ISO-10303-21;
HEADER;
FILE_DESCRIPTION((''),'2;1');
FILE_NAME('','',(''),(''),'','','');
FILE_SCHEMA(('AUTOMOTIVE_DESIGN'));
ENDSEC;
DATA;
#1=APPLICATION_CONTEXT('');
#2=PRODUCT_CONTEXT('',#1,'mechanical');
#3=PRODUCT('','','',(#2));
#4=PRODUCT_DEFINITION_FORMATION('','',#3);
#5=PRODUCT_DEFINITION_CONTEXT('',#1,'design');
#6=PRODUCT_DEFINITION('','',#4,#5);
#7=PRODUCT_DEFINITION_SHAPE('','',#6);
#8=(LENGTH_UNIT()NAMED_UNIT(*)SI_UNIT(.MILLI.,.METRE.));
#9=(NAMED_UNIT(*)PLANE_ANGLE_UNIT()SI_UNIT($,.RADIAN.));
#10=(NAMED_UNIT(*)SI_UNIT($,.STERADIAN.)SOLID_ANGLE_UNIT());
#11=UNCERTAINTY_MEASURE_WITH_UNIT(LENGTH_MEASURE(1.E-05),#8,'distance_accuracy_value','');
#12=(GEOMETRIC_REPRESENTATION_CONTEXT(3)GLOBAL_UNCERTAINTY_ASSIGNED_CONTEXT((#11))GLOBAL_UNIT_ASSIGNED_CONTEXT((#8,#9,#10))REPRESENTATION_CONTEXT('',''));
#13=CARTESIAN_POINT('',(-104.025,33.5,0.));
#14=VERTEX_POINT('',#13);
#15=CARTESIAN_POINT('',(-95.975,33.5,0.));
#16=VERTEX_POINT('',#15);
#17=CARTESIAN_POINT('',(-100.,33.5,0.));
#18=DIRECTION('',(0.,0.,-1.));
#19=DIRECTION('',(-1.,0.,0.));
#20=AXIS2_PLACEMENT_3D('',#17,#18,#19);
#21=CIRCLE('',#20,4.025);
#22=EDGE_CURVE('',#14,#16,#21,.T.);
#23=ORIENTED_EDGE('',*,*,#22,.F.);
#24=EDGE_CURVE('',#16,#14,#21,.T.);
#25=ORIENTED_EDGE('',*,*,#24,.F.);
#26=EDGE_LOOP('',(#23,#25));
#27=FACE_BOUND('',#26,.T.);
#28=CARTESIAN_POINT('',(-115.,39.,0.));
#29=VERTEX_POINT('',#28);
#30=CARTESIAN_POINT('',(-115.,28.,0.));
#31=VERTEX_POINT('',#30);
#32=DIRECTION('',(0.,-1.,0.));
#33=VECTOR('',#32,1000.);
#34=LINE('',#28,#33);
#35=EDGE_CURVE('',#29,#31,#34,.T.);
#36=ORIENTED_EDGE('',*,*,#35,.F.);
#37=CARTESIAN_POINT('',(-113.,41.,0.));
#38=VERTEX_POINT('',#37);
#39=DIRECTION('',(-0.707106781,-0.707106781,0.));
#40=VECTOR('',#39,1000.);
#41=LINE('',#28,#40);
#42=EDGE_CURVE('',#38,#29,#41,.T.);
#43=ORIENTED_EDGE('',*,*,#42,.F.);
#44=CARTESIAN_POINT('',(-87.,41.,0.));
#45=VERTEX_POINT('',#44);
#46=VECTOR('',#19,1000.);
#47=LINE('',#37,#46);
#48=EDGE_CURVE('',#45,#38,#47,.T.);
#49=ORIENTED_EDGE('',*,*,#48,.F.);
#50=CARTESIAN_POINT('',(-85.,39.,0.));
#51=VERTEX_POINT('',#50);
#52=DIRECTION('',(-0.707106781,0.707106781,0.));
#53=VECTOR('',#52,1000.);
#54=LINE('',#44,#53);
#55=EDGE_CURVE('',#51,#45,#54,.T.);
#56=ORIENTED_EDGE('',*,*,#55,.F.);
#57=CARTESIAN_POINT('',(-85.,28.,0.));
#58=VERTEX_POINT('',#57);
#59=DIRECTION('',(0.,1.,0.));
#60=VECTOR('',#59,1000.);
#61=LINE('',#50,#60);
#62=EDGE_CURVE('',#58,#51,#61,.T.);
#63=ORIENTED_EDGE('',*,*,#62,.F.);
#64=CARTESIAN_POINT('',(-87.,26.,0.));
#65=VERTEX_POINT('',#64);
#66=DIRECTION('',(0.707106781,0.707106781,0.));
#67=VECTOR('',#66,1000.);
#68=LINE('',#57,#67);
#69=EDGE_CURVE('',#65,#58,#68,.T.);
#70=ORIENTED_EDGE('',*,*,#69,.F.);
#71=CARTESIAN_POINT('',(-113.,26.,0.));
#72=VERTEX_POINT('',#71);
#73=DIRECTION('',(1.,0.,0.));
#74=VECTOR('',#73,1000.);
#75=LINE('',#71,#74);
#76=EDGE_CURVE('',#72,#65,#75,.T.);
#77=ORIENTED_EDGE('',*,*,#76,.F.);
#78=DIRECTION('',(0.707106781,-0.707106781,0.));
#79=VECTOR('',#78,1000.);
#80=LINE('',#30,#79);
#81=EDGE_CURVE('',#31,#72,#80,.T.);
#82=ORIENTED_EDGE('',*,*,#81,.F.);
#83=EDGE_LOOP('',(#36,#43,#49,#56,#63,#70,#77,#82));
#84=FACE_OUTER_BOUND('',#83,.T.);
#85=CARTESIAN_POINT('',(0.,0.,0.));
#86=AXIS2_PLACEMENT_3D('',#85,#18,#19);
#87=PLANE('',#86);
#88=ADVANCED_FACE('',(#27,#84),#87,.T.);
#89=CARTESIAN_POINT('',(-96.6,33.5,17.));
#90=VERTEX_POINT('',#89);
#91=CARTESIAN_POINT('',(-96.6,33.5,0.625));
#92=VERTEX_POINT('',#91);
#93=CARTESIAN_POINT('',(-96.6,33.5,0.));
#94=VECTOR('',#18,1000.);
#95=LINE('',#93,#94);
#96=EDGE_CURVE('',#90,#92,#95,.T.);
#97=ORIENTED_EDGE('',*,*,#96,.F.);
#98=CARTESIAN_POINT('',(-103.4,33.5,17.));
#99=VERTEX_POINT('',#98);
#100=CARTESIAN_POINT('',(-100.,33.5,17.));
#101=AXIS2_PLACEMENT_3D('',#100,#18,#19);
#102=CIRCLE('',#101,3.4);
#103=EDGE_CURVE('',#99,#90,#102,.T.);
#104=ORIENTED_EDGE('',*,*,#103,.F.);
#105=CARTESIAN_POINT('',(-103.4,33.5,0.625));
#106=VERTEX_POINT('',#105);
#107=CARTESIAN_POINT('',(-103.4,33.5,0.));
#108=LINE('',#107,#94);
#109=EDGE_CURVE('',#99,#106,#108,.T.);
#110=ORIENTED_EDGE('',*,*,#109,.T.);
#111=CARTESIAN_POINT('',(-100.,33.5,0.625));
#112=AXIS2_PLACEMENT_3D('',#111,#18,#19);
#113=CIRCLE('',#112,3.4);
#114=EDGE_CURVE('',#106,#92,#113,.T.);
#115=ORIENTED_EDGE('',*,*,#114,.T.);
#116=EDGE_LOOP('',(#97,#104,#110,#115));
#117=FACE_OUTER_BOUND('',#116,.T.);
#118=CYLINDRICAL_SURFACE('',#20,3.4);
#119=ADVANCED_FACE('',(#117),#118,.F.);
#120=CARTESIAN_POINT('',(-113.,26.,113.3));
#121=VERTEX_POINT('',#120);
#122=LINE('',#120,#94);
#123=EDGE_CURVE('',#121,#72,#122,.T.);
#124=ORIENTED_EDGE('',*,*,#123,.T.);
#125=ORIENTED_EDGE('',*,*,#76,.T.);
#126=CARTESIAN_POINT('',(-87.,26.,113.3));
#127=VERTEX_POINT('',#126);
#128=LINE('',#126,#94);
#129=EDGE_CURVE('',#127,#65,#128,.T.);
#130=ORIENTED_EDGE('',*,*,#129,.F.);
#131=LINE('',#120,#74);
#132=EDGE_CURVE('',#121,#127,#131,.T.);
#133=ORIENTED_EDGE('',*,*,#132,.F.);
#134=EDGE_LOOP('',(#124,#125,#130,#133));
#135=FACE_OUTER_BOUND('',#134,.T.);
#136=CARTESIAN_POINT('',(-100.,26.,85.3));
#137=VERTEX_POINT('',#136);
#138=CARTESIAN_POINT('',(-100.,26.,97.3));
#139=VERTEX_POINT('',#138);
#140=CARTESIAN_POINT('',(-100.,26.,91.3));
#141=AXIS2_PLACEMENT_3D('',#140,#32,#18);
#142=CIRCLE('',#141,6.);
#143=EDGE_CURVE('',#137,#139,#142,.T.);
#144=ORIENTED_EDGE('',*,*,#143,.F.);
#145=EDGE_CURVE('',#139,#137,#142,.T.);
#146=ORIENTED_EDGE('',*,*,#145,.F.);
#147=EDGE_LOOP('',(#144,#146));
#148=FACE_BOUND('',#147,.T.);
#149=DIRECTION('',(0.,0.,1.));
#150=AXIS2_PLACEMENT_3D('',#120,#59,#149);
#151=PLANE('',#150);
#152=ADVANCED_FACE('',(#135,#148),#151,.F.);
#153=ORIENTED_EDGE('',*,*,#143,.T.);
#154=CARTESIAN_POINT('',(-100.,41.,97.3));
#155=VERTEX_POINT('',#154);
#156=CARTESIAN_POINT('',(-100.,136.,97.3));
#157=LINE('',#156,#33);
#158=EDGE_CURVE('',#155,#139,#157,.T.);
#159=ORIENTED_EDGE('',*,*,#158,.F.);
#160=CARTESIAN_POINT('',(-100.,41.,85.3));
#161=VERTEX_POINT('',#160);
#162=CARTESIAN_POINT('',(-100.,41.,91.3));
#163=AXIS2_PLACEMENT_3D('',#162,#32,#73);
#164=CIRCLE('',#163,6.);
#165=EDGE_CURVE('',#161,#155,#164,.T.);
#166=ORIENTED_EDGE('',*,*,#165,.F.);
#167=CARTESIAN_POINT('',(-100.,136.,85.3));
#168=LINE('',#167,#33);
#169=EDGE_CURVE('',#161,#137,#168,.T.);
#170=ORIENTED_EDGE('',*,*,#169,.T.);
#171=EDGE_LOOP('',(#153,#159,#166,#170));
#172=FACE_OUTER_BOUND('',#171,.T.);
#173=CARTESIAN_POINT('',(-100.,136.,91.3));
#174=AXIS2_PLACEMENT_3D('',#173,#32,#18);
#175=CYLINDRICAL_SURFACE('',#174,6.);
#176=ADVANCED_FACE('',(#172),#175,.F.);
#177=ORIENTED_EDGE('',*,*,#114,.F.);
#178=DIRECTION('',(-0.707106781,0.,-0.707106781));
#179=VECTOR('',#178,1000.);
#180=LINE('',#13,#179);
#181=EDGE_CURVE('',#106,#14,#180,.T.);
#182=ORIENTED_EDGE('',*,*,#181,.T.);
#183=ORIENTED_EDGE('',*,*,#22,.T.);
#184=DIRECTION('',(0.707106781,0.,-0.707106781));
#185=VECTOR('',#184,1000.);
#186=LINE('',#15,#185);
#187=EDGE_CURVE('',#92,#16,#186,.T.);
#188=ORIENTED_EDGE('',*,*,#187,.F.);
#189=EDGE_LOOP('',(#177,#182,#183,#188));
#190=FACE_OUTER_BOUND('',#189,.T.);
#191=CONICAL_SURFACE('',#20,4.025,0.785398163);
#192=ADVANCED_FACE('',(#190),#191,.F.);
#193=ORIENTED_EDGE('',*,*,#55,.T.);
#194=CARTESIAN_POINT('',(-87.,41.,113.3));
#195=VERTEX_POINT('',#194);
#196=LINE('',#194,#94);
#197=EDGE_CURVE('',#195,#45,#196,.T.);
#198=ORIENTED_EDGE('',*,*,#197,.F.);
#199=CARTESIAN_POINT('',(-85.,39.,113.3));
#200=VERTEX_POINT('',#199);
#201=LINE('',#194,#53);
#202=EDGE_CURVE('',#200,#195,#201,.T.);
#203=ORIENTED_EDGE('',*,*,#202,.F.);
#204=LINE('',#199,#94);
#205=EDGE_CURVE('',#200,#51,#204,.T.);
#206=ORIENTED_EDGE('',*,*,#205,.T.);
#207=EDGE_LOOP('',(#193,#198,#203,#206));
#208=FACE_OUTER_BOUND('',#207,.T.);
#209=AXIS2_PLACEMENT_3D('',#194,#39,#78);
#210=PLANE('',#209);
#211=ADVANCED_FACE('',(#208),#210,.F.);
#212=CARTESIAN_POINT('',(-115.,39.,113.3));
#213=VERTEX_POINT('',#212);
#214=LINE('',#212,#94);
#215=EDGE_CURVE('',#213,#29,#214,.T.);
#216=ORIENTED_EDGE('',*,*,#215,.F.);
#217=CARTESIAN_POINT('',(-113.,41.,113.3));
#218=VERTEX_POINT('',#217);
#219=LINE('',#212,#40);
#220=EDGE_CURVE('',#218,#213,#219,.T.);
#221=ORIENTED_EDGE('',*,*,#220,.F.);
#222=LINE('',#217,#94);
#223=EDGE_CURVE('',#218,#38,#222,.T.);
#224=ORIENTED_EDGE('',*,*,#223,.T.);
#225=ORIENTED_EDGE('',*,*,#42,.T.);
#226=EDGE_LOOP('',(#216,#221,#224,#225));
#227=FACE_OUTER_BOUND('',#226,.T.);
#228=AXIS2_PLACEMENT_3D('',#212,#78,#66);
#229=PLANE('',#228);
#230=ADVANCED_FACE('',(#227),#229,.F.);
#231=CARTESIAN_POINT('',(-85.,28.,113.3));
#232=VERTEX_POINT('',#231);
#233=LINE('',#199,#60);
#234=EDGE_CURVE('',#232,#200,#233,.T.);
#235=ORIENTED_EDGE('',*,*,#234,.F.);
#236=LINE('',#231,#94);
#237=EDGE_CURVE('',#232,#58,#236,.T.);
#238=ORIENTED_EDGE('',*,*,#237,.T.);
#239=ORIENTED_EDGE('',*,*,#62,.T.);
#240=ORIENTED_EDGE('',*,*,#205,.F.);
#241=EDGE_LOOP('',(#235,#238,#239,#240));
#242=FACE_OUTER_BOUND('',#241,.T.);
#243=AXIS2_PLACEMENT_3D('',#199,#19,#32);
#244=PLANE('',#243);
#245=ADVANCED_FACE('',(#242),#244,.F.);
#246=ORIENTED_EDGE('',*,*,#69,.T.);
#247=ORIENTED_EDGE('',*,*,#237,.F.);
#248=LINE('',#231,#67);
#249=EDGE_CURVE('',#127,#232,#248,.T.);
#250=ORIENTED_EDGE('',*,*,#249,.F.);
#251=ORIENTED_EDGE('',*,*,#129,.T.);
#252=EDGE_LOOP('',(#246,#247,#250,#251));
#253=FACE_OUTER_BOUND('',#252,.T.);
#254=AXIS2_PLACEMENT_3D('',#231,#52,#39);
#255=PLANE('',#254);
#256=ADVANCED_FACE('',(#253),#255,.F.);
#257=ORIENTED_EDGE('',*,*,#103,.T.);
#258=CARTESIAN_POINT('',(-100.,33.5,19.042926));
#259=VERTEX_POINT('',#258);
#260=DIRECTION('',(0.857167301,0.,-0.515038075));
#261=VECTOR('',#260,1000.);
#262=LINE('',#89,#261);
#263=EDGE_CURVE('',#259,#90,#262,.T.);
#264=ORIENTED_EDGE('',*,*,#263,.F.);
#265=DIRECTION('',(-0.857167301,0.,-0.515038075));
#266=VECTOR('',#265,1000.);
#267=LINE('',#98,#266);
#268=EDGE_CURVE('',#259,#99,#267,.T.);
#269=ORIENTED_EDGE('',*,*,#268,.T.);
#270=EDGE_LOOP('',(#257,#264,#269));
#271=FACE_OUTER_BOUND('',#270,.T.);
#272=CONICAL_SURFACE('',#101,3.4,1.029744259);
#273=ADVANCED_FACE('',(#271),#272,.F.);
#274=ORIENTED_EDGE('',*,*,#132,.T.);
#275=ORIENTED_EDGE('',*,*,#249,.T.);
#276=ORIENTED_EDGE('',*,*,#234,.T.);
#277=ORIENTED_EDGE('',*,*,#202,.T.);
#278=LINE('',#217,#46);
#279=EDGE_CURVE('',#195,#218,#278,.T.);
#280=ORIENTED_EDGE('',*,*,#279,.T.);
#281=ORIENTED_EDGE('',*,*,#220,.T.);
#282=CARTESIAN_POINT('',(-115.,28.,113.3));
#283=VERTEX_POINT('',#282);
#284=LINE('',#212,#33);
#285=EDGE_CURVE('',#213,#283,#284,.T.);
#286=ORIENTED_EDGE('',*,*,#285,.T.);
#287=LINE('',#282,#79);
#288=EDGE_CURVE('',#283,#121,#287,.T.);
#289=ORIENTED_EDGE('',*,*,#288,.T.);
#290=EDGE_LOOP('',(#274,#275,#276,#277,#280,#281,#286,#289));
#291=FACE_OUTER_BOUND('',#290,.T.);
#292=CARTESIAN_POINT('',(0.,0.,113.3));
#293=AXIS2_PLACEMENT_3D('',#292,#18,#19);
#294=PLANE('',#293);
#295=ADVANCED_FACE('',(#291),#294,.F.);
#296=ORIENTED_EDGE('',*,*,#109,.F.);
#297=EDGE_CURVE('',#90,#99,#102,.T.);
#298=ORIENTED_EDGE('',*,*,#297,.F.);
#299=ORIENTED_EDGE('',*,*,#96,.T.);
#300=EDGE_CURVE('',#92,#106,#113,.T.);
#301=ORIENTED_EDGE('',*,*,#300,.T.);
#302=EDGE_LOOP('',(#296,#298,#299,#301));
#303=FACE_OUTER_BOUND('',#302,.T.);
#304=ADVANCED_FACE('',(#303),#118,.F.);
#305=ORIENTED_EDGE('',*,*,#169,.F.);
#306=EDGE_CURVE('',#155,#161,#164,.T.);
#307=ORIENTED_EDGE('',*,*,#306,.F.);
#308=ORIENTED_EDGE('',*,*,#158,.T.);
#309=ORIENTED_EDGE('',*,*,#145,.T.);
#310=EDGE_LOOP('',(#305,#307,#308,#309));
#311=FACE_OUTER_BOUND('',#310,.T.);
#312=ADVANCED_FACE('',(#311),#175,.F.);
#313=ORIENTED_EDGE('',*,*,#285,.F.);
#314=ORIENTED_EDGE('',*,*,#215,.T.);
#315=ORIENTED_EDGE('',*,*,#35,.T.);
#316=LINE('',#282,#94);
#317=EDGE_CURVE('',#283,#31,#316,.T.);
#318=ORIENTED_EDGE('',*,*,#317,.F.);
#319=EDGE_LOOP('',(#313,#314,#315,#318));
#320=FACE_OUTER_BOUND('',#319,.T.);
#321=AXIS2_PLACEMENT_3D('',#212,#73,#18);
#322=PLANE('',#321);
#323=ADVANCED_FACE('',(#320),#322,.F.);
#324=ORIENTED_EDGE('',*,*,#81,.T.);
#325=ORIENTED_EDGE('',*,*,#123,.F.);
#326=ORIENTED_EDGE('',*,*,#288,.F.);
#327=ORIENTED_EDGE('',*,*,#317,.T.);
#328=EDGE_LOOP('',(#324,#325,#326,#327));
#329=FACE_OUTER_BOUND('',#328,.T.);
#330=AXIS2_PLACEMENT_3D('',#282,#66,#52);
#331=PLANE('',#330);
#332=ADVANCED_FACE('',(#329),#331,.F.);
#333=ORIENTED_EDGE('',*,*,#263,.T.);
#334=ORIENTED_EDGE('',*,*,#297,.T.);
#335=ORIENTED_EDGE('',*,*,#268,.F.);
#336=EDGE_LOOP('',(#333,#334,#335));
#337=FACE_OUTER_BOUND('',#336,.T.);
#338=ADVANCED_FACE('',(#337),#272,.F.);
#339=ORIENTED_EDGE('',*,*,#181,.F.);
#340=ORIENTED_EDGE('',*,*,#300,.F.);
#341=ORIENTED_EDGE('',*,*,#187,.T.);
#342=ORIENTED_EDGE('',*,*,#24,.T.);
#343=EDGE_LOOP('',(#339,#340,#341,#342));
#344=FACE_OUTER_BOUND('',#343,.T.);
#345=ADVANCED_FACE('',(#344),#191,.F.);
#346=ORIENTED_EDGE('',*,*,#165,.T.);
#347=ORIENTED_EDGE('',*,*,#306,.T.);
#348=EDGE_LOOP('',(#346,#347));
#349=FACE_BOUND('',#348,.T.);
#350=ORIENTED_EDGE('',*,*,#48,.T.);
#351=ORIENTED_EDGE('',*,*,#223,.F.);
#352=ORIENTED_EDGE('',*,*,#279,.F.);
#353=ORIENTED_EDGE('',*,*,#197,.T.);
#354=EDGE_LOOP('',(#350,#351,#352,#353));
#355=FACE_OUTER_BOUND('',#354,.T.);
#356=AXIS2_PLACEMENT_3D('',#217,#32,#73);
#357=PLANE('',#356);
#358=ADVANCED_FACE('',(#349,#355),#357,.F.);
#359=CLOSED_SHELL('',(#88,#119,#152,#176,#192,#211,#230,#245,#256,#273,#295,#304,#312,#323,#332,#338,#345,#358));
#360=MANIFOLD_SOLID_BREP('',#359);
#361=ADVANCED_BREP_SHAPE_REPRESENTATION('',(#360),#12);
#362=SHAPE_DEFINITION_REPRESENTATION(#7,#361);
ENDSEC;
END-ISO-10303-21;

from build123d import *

# Parameters (mm, degrees)
BOSS_EXTRUDE1_DEPTH          = 113.3
SKETCH2_R                    = 6
CUT_EXTRUDE1_DEPTH           = 110
M8_TAPPED_HOLE_1_D           = 6.8
M8_TAPPED_HOLE_1_DEPTH       = 17
M8_TAPPED_HOLE_1_CSINK_D     = 8.05
M8_TAPPED_HOLE_1_CSINK_ANGLE = 90
M8_TAPPED_HOLE_1_TIP         = 2.042926105


with BuildPart() as part:
    # Sketch1 → Boss-Extrude1 (new body)
    with BuildSketch(Plane.XY):
        Polygon((-113, 41), (-87, 41), (-85, 39), (-85, 28), (-87, 26), (-113, 26), (-115, 28), (-115, 39), align=None)
    extrude(amount=BOSS_EXTRUDE1_DEPTH)

    # Sketch2 → Cut-Extrude1 (cut)
    with BuildSketch(Plane(origin=(0, 26, 0), x_dir=(-1, 0, 0), z_dir=(0, -1, 0))):
        with Locations(Location((100, -91.3, 0), (0, 0, 90))):
            Circle(SKETCH2_R)
    extrude(amount=-CUT_EXTRUDE1_DEPTH, mode=Mode.SUBTRACT)

    # M8 Tapped Hole 1
    with Locations(Plane(origin=(0, 0, 0), x_dir=(-1, 0, 0), z_dir=(0, 0, -1))):
        with Locations((100, 33.5)):
            CounterSinkHole(M8_TAPPED_HOLE_1_D / 2, M8_TAPPED_HOLE_1_CSINK_D / 2, depth=M8_TAPPED_HOLE_1_DEPTH, counter_sink_angle=M8_TAPPED_HOLE_1_CSINK_ANGLE)
            with Locations((0, 0, -(M8_TAPPED_HOLE_1_DEPTH + M8_TAPPED_HOLE_1_TIP / 2))):  # 118° drill point
                Cone(0, M8_TAPPED_HOLE_1_D / 2, M8_TAPPED_HOLE_1_TIP, mode=Mode.SUBTRACT)


solid = part.part
